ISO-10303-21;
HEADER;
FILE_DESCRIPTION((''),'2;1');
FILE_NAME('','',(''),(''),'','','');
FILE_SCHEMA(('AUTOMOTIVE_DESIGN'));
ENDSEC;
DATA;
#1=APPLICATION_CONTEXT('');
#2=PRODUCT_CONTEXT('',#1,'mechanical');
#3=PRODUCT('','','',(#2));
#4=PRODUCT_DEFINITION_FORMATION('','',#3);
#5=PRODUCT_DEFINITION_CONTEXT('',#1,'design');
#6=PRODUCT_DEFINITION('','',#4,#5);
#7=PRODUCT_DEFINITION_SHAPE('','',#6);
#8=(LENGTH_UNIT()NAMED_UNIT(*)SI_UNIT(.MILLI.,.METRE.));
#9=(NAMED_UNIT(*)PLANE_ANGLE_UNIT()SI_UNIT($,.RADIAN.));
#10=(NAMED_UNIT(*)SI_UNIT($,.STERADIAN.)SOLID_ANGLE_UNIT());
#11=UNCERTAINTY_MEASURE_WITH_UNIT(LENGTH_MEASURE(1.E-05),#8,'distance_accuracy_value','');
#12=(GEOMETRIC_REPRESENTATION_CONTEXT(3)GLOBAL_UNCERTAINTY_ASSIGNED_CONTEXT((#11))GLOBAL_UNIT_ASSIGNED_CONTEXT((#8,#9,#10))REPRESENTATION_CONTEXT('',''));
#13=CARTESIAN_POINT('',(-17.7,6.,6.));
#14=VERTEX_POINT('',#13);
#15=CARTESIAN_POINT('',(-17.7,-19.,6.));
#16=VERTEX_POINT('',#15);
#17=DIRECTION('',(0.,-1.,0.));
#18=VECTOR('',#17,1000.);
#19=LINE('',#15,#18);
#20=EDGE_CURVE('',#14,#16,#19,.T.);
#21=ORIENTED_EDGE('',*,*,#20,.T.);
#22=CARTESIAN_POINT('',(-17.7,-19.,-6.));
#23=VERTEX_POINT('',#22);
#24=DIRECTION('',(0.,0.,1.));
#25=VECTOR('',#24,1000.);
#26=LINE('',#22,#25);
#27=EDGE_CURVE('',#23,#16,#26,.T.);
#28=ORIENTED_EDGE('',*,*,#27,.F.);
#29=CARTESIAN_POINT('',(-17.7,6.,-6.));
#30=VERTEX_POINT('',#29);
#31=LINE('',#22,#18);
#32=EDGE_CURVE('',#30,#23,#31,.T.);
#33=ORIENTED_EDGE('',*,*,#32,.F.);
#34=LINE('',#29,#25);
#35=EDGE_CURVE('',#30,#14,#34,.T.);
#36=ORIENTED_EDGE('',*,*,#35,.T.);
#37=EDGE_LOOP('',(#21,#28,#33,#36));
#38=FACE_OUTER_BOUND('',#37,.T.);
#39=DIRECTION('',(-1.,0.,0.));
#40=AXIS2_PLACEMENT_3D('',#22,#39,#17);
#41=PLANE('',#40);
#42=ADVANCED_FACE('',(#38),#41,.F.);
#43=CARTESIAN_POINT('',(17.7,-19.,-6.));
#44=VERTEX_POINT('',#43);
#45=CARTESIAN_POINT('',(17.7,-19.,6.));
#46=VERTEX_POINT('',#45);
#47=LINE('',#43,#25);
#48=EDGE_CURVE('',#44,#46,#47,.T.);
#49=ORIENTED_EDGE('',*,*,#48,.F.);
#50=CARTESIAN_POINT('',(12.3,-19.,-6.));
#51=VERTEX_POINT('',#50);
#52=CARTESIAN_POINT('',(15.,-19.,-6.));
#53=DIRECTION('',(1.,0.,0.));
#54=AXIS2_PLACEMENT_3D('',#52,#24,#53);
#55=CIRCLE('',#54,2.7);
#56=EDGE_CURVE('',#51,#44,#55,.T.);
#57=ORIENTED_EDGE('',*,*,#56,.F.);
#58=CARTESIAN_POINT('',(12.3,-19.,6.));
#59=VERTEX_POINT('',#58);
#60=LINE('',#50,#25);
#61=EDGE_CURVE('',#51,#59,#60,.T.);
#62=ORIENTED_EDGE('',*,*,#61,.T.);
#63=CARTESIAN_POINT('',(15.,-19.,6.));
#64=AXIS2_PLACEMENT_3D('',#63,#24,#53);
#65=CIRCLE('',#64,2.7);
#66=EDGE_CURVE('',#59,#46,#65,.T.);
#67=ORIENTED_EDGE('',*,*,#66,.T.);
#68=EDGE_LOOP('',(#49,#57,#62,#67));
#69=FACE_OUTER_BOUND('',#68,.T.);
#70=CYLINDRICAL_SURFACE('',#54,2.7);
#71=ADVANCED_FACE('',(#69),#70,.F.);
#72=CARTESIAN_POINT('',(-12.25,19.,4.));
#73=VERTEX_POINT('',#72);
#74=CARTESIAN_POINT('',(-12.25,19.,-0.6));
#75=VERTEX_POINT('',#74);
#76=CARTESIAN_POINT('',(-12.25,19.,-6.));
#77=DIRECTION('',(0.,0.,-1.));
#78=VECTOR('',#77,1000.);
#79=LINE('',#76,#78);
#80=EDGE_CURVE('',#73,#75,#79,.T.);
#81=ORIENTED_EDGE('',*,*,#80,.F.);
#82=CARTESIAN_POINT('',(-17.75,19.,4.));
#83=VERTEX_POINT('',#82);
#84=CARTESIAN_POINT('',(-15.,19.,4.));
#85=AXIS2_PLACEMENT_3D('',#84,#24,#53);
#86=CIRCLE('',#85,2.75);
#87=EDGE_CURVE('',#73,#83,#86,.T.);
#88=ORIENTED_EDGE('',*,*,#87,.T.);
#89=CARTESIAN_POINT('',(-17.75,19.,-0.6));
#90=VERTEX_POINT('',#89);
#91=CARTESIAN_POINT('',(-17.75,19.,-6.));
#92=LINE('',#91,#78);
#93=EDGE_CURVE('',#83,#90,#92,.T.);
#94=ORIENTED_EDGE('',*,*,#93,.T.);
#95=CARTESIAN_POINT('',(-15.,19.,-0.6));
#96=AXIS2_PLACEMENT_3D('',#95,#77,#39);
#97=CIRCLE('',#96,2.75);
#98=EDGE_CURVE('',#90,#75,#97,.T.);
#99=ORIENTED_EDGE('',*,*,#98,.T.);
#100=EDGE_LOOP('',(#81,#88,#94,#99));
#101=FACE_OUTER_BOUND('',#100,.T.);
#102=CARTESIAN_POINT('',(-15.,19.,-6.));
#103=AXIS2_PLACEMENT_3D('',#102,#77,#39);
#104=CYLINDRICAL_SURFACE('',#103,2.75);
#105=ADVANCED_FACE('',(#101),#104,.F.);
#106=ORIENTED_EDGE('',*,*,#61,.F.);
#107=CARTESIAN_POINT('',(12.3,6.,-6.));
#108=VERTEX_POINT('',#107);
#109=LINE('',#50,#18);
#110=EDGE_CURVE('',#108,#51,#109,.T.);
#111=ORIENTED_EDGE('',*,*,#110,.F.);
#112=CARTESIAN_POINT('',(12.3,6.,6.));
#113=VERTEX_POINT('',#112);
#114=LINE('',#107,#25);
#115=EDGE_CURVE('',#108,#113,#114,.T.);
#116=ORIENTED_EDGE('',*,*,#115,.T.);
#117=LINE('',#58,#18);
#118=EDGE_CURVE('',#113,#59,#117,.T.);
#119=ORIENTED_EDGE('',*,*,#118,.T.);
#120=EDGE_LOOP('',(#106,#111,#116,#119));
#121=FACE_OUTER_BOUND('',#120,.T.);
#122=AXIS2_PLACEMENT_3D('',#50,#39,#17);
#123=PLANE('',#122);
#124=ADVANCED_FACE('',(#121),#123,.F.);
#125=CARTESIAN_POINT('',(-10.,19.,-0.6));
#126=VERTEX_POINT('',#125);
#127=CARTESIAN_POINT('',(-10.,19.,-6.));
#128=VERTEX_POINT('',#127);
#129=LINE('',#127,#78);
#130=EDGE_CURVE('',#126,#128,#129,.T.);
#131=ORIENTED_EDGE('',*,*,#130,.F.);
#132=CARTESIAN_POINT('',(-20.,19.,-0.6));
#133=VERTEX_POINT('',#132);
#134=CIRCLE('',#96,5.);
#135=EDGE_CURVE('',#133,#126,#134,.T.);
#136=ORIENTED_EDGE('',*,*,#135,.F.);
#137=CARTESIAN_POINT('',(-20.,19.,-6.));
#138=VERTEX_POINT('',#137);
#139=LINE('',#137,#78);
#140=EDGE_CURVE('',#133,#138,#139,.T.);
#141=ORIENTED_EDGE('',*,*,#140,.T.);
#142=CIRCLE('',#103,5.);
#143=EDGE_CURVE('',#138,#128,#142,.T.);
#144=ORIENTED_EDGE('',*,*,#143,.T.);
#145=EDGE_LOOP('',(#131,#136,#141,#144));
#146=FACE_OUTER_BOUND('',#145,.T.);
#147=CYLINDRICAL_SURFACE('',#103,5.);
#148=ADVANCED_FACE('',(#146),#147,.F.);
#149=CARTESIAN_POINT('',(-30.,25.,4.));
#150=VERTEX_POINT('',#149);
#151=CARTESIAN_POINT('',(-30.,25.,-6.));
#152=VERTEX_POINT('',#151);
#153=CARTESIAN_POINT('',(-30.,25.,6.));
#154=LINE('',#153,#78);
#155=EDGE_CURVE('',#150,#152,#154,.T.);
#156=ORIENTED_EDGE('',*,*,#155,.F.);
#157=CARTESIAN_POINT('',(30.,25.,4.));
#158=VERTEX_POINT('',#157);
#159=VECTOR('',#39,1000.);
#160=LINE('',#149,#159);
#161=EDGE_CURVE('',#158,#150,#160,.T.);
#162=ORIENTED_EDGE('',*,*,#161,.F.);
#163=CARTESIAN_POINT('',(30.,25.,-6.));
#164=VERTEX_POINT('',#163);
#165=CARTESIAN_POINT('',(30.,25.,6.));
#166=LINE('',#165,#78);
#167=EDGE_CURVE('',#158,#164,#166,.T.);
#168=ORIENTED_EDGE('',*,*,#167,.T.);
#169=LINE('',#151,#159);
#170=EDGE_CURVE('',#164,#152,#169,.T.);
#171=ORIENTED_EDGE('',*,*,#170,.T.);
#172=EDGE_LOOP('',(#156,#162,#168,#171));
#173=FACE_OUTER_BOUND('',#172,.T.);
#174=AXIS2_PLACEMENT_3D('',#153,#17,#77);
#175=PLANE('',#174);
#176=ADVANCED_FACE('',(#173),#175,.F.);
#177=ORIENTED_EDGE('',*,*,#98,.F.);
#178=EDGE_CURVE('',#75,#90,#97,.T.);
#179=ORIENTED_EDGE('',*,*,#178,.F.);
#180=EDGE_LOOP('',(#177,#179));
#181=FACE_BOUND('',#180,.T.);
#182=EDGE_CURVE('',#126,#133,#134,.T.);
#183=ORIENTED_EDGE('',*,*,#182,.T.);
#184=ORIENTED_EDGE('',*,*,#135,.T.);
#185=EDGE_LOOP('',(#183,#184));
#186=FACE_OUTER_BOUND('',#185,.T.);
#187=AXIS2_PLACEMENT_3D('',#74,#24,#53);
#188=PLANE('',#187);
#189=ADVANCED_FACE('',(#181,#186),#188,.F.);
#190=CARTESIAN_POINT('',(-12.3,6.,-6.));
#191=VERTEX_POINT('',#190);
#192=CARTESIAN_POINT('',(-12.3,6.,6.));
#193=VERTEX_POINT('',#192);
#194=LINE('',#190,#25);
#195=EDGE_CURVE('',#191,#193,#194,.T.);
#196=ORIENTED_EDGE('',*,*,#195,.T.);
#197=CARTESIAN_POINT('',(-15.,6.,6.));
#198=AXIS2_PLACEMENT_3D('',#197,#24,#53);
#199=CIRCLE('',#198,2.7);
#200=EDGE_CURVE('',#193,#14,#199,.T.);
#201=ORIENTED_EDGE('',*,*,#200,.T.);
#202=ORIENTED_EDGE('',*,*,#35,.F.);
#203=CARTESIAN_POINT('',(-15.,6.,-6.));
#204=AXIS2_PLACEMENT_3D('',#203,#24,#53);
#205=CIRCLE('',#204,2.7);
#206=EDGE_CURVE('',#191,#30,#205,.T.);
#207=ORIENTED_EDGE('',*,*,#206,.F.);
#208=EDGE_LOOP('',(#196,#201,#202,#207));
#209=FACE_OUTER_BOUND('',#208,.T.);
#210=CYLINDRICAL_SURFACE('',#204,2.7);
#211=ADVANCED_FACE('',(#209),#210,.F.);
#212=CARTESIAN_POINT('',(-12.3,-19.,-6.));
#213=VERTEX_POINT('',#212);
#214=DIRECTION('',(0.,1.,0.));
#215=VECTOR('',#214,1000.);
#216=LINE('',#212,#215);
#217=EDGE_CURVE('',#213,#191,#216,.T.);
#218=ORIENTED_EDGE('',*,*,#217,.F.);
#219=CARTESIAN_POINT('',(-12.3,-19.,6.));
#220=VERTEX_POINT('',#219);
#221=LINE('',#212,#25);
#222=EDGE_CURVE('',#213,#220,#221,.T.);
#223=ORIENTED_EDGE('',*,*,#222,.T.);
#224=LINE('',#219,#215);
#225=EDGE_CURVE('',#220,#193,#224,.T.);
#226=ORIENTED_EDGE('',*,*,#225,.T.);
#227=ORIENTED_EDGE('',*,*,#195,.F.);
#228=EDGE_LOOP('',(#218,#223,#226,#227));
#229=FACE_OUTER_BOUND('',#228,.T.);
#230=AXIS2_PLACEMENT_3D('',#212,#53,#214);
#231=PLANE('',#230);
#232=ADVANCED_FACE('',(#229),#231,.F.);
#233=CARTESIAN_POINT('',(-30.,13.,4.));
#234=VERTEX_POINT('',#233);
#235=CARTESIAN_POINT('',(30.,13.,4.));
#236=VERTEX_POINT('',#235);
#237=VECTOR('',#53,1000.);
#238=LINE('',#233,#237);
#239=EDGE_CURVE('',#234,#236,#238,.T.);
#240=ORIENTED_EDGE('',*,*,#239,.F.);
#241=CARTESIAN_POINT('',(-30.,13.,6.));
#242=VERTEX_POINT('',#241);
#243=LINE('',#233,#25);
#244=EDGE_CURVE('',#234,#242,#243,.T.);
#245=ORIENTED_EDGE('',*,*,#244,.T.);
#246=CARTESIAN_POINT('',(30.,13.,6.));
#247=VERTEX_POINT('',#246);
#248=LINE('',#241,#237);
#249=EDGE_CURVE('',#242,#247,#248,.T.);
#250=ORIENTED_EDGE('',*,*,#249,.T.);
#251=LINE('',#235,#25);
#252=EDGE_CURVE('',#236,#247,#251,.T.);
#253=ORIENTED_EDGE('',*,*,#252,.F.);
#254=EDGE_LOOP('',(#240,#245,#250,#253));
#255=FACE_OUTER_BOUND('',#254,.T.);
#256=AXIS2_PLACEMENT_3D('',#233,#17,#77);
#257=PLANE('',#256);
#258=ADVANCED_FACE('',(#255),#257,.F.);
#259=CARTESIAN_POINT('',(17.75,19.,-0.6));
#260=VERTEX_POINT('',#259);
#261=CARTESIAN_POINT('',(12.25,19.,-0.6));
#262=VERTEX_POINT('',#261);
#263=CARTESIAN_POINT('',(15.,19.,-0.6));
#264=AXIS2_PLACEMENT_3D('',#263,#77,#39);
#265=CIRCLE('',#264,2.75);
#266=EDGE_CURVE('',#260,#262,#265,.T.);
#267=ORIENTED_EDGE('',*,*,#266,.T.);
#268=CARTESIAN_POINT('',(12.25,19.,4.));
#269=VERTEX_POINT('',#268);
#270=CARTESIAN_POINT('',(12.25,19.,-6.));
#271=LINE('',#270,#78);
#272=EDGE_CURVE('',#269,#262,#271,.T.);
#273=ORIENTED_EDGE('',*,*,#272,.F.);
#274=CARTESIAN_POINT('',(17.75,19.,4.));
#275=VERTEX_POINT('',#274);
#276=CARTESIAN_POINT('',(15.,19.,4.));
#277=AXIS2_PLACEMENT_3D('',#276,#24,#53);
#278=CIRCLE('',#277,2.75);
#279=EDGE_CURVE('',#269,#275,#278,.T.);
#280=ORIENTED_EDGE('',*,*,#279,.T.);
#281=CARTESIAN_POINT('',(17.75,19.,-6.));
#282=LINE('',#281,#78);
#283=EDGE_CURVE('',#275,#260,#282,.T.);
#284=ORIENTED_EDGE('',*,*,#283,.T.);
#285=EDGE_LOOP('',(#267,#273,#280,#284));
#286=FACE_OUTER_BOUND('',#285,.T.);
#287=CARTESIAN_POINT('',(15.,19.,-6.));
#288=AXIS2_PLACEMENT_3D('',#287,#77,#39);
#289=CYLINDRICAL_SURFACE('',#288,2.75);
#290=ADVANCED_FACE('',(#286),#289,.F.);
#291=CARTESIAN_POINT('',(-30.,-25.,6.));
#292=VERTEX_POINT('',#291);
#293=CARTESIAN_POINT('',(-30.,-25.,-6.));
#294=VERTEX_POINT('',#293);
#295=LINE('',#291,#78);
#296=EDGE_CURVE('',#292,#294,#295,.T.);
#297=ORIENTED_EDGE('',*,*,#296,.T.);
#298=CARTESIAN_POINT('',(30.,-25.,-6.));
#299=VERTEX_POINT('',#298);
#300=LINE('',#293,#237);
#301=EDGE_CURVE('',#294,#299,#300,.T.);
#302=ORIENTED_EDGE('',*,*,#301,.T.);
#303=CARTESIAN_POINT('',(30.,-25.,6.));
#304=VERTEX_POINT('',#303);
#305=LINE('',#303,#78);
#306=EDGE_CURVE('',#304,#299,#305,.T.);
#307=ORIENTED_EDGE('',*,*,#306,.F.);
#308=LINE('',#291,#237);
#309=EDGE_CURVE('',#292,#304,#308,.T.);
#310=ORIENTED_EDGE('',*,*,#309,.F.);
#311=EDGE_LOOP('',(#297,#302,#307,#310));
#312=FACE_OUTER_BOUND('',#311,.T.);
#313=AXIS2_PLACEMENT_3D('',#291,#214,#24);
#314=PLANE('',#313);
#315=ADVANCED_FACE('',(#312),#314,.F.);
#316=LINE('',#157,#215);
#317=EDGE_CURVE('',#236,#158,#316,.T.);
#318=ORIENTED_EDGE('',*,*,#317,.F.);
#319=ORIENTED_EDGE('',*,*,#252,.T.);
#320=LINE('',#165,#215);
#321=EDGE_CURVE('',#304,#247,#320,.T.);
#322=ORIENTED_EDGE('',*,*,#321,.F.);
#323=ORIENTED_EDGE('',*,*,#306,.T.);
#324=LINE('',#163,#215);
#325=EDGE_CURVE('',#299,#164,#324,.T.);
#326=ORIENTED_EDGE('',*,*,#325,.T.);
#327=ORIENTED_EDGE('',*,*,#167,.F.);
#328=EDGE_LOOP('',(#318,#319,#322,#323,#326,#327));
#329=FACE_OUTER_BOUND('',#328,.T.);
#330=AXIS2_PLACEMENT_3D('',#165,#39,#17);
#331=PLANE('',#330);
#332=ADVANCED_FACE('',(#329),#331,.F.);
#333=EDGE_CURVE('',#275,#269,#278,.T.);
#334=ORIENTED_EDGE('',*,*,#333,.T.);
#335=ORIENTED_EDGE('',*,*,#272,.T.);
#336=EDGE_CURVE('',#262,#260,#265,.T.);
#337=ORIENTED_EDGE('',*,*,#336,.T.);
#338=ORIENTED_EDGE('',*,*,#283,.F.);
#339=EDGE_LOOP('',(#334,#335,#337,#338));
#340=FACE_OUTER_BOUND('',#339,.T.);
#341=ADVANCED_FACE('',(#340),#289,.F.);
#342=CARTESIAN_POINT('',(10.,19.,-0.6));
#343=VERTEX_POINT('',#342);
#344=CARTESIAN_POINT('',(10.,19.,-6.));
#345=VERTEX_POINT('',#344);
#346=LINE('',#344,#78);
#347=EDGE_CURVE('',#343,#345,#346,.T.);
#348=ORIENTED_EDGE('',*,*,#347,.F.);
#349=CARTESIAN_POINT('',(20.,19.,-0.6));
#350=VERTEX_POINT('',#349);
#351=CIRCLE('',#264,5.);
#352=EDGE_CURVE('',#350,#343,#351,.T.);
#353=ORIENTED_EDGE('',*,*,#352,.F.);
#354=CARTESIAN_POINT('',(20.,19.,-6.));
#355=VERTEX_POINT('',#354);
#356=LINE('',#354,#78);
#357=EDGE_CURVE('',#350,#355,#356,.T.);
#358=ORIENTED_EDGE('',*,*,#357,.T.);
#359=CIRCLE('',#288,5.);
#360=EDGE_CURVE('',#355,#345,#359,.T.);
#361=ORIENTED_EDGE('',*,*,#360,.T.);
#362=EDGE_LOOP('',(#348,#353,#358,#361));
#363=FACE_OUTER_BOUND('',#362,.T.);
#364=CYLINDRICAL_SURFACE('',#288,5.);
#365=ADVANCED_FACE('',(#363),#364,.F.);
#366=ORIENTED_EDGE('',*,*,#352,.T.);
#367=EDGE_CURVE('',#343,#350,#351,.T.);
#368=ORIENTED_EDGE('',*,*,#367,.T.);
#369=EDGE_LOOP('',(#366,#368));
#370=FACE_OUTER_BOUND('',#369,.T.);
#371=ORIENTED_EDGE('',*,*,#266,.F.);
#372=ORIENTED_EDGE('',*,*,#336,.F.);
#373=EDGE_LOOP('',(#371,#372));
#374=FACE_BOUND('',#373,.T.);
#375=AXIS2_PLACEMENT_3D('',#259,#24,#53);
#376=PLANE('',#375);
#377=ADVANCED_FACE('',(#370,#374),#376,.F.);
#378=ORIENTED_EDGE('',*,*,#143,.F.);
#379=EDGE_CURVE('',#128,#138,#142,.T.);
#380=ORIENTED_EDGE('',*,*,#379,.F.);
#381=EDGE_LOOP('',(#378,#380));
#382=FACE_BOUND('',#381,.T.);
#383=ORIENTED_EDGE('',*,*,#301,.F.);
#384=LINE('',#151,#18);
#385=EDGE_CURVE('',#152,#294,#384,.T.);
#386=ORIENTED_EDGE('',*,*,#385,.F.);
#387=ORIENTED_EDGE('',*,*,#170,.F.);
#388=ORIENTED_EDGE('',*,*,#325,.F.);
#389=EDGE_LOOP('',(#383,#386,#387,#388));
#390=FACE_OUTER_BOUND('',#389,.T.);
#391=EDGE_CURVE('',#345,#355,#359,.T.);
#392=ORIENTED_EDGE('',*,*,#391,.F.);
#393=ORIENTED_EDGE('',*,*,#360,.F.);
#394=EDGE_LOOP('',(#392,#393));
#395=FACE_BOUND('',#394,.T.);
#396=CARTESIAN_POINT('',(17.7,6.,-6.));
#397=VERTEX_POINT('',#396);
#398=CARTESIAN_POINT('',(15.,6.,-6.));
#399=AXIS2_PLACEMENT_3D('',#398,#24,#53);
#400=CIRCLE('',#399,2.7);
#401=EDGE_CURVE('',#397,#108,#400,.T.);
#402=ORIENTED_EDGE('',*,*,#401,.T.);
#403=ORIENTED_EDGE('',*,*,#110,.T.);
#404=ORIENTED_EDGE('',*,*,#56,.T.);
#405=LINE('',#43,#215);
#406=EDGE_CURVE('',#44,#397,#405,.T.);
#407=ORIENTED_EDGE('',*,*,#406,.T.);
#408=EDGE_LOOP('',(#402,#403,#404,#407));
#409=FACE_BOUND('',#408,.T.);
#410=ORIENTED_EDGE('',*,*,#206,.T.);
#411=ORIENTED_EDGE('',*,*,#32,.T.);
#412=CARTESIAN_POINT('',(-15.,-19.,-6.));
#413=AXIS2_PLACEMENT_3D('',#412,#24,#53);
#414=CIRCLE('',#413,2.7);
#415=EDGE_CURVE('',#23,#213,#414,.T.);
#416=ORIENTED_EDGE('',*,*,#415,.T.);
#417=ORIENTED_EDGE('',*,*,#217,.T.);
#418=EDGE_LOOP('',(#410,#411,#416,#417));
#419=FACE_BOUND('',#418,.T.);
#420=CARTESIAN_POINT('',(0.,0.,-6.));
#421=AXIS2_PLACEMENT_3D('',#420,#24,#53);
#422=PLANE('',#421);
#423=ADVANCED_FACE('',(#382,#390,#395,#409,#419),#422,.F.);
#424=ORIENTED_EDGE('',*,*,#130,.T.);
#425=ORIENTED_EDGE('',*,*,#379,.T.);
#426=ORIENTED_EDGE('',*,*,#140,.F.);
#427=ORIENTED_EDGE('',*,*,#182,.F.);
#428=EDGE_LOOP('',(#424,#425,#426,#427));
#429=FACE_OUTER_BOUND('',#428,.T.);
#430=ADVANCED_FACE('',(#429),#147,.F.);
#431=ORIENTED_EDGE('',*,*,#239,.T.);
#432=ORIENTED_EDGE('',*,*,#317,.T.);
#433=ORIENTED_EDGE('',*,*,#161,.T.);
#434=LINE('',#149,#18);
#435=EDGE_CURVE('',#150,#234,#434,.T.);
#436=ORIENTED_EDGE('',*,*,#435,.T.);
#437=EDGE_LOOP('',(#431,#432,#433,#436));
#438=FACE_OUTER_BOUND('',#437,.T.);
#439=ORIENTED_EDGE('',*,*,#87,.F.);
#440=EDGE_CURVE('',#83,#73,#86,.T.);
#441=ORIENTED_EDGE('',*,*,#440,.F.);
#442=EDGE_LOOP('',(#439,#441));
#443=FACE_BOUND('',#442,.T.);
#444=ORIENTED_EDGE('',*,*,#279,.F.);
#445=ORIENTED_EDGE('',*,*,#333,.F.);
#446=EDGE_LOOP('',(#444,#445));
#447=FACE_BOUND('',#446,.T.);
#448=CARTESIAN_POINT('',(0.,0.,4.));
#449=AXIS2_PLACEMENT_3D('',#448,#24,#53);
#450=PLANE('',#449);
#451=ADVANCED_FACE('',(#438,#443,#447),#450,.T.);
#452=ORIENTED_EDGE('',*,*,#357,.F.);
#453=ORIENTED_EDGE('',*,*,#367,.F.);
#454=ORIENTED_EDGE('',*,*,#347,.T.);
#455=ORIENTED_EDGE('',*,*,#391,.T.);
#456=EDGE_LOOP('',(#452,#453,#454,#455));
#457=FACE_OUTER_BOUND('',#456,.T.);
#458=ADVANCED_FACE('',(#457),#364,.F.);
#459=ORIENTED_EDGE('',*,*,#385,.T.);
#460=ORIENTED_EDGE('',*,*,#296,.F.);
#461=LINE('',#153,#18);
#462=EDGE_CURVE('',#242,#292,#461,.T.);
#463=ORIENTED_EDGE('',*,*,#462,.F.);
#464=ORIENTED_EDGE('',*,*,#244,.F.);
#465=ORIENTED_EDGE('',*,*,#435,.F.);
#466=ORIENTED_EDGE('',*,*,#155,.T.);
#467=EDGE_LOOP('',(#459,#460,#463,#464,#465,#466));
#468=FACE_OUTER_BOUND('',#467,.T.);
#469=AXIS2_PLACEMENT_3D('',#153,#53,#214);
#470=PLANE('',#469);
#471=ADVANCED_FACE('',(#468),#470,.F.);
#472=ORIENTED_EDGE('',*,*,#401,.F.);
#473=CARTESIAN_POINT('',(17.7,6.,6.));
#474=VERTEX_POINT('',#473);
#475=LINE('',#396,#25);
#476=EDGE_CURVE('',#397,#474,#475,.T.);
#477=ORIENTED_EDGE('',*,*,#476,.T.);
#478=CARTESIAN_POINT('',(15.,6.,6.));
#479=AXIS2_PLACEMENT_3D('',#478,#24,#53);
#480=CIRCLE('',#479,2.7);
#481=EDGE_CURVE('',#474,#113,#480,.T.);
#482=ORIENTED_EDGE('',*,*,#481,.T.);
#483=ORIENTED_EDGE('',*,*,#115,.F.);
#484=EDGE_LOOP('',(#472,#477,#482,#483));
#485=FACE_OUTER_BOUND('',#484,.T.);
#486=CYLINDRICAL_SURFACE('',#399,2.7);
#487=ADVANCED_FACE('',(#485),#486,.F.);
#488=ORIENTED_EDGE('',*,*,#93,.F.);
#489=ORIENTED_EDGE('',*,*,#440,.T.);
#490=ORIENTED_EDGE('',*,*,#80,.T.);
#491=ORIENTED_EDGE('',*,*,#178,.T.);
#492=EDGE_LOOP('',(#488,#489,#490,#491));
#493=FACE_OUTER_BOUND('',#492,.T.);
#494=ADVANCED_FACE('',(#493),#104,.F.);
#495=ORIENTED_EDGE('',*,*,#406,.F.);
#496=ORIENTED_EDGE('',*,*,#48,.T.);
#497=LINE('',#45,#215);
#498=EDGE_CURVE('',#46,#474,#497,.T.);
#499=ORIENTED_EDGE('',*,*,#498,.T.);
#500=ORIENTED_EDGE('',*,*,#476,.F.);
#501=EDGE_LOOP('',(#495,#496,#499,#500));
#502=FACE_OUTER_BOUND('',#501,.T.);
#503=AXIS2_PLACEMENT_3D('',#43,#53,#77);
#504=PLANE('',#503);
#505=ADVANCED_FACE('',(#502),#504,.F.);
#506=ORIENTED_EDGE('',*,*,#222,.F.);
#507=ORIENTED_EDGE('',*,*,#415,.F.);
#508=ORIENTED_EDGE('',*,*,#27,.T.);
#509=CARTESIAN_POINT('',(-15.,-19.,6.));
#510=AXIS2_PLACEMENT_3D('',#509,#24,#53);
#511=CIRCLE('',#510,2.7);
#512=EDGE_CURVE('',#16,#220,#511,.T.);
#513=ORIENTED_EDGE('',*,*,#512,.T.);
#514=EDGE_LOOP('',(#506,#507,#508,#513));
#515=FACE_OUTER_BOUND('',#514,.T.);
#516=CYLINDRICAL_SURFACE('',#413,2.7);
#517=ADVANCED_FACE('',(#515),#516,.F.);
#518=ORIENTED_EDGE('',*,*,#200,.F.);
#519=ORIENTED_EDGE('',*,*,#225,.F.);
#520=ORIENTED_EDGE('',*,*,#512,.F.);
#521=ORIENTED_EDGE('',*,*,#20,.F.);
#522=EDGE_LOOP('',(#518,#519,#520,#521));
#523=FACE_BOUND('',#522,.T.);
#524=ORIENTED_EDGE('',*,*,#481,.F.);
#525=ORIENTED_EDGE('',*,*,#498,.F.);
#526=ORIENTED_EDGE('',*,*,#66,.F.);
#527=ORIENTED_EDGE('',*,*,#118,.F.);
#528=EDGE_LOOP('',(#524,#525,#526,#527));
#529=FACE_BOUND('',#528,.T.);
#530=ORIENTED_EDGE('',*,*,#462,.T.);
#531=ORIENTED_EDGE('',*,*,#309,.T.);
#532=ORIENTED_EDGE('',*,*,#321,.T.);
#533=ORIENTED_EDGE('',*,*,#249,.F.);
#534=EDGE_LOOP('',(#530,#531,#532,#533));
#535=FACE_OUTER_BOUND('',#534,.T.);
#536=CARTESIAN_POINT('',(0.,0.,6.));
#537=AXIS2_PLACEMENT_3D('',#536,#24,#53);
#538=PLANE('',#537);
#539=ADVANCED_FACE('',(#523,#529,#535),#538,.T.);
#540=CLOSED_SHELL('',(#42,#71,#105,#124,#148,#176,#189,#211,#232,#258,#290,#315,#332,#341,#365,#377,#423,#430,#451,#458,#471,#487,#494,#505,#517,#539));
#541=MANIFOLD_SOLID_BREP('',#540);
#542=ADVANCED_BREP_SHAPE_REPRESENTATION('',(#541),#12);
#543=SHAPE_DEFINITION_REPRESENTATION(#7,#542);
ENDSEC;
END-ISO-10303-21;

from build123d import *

# Parameters (mm, degrees)
SKETCH_1_W                   = 60
SKETCH_1_H                   = 50
EXTRUDE_1_DEPTH              = 6
SKETCH_2_W                   = 60
SKETCH_2_H                   = 12
CUT_EXTRUDE_1_DEPTH          = 2
CUT_EXTRUDE_2_DEPTH          = 41.853396432
HOLE_WIZARD_M4_1_D           = 5.5
HOLE_WIZARD_M4_1_CBORE_D     = 10
HOLE_WIZARD_M4_1_CBORE_DEPTH = 5.4


with BuildPart() as part:
    # 草图1 → 凸台-拉伸1 (new, symmetric)
    with BuildSketch(Plane.XY):
        Rectangle(SKETCH_1_W, SKETCH_1_H)
    extrude(amount=EXTRUDE_1_DEPTH, both=True)

    # 草图2 → 切除-拉伸1 (cut)
    with BuildSketch(Plane.XY.offset(6)):
        with Locations((0, 19)):
            Rectangle(SKETCH_2_W, SKETCH_2_H)
    extrude(amount=-CUT_EXTRUDE_1_DEPTH, mode=Mode.SUBTRACT)

    # 草图3 → 切除-拉伸2 (cut, through all)
    with BuildSketch(Plane.XY.offset(6)):
        with BuildLine():
            Line((-17.7, -19), (-17.7, 6))
            ThreePointArc((-17.7, 6), (-15, 8.7), (-12.3, 6))
            Line((-12.3, 6), (-12.3, -19))
            ThreePointArc((-12.3, -19), (-15, -21.7), (-17.7, -19))
        make_face()
        with BuildLine():
            Line((12.3, -19), (12.3, 6))
            ThreePointArc((12.3, 6), (15, 8.7), (17.7, 6))
            Line((17.7, 6), (17.7, -19))
            ThreePointArc((17.7, -19), (15, -21.7), (12.3, -19))
        make_face()
    extrude(amount=-CUT_EXTRUDE_2_DEPTH, mode=Mode.SUBTRACT)

    # M4 沉头孔1 (through all)
    with Locations(Plane(origin=(0, 0, -6), x_dir=(-1, 0, 0), z_dir=(0, 0, -1))):
        with Locations((-15, 19), (15, 19)):
            CounterBoreHole(HOLE_WIZARD_M4_1_D / 2, HOLE_WIZARD_M4_1_CBORE_D / 2, HOLE_WIZARD_M4_1_CBORE_DEPTH)


solid = part.part
